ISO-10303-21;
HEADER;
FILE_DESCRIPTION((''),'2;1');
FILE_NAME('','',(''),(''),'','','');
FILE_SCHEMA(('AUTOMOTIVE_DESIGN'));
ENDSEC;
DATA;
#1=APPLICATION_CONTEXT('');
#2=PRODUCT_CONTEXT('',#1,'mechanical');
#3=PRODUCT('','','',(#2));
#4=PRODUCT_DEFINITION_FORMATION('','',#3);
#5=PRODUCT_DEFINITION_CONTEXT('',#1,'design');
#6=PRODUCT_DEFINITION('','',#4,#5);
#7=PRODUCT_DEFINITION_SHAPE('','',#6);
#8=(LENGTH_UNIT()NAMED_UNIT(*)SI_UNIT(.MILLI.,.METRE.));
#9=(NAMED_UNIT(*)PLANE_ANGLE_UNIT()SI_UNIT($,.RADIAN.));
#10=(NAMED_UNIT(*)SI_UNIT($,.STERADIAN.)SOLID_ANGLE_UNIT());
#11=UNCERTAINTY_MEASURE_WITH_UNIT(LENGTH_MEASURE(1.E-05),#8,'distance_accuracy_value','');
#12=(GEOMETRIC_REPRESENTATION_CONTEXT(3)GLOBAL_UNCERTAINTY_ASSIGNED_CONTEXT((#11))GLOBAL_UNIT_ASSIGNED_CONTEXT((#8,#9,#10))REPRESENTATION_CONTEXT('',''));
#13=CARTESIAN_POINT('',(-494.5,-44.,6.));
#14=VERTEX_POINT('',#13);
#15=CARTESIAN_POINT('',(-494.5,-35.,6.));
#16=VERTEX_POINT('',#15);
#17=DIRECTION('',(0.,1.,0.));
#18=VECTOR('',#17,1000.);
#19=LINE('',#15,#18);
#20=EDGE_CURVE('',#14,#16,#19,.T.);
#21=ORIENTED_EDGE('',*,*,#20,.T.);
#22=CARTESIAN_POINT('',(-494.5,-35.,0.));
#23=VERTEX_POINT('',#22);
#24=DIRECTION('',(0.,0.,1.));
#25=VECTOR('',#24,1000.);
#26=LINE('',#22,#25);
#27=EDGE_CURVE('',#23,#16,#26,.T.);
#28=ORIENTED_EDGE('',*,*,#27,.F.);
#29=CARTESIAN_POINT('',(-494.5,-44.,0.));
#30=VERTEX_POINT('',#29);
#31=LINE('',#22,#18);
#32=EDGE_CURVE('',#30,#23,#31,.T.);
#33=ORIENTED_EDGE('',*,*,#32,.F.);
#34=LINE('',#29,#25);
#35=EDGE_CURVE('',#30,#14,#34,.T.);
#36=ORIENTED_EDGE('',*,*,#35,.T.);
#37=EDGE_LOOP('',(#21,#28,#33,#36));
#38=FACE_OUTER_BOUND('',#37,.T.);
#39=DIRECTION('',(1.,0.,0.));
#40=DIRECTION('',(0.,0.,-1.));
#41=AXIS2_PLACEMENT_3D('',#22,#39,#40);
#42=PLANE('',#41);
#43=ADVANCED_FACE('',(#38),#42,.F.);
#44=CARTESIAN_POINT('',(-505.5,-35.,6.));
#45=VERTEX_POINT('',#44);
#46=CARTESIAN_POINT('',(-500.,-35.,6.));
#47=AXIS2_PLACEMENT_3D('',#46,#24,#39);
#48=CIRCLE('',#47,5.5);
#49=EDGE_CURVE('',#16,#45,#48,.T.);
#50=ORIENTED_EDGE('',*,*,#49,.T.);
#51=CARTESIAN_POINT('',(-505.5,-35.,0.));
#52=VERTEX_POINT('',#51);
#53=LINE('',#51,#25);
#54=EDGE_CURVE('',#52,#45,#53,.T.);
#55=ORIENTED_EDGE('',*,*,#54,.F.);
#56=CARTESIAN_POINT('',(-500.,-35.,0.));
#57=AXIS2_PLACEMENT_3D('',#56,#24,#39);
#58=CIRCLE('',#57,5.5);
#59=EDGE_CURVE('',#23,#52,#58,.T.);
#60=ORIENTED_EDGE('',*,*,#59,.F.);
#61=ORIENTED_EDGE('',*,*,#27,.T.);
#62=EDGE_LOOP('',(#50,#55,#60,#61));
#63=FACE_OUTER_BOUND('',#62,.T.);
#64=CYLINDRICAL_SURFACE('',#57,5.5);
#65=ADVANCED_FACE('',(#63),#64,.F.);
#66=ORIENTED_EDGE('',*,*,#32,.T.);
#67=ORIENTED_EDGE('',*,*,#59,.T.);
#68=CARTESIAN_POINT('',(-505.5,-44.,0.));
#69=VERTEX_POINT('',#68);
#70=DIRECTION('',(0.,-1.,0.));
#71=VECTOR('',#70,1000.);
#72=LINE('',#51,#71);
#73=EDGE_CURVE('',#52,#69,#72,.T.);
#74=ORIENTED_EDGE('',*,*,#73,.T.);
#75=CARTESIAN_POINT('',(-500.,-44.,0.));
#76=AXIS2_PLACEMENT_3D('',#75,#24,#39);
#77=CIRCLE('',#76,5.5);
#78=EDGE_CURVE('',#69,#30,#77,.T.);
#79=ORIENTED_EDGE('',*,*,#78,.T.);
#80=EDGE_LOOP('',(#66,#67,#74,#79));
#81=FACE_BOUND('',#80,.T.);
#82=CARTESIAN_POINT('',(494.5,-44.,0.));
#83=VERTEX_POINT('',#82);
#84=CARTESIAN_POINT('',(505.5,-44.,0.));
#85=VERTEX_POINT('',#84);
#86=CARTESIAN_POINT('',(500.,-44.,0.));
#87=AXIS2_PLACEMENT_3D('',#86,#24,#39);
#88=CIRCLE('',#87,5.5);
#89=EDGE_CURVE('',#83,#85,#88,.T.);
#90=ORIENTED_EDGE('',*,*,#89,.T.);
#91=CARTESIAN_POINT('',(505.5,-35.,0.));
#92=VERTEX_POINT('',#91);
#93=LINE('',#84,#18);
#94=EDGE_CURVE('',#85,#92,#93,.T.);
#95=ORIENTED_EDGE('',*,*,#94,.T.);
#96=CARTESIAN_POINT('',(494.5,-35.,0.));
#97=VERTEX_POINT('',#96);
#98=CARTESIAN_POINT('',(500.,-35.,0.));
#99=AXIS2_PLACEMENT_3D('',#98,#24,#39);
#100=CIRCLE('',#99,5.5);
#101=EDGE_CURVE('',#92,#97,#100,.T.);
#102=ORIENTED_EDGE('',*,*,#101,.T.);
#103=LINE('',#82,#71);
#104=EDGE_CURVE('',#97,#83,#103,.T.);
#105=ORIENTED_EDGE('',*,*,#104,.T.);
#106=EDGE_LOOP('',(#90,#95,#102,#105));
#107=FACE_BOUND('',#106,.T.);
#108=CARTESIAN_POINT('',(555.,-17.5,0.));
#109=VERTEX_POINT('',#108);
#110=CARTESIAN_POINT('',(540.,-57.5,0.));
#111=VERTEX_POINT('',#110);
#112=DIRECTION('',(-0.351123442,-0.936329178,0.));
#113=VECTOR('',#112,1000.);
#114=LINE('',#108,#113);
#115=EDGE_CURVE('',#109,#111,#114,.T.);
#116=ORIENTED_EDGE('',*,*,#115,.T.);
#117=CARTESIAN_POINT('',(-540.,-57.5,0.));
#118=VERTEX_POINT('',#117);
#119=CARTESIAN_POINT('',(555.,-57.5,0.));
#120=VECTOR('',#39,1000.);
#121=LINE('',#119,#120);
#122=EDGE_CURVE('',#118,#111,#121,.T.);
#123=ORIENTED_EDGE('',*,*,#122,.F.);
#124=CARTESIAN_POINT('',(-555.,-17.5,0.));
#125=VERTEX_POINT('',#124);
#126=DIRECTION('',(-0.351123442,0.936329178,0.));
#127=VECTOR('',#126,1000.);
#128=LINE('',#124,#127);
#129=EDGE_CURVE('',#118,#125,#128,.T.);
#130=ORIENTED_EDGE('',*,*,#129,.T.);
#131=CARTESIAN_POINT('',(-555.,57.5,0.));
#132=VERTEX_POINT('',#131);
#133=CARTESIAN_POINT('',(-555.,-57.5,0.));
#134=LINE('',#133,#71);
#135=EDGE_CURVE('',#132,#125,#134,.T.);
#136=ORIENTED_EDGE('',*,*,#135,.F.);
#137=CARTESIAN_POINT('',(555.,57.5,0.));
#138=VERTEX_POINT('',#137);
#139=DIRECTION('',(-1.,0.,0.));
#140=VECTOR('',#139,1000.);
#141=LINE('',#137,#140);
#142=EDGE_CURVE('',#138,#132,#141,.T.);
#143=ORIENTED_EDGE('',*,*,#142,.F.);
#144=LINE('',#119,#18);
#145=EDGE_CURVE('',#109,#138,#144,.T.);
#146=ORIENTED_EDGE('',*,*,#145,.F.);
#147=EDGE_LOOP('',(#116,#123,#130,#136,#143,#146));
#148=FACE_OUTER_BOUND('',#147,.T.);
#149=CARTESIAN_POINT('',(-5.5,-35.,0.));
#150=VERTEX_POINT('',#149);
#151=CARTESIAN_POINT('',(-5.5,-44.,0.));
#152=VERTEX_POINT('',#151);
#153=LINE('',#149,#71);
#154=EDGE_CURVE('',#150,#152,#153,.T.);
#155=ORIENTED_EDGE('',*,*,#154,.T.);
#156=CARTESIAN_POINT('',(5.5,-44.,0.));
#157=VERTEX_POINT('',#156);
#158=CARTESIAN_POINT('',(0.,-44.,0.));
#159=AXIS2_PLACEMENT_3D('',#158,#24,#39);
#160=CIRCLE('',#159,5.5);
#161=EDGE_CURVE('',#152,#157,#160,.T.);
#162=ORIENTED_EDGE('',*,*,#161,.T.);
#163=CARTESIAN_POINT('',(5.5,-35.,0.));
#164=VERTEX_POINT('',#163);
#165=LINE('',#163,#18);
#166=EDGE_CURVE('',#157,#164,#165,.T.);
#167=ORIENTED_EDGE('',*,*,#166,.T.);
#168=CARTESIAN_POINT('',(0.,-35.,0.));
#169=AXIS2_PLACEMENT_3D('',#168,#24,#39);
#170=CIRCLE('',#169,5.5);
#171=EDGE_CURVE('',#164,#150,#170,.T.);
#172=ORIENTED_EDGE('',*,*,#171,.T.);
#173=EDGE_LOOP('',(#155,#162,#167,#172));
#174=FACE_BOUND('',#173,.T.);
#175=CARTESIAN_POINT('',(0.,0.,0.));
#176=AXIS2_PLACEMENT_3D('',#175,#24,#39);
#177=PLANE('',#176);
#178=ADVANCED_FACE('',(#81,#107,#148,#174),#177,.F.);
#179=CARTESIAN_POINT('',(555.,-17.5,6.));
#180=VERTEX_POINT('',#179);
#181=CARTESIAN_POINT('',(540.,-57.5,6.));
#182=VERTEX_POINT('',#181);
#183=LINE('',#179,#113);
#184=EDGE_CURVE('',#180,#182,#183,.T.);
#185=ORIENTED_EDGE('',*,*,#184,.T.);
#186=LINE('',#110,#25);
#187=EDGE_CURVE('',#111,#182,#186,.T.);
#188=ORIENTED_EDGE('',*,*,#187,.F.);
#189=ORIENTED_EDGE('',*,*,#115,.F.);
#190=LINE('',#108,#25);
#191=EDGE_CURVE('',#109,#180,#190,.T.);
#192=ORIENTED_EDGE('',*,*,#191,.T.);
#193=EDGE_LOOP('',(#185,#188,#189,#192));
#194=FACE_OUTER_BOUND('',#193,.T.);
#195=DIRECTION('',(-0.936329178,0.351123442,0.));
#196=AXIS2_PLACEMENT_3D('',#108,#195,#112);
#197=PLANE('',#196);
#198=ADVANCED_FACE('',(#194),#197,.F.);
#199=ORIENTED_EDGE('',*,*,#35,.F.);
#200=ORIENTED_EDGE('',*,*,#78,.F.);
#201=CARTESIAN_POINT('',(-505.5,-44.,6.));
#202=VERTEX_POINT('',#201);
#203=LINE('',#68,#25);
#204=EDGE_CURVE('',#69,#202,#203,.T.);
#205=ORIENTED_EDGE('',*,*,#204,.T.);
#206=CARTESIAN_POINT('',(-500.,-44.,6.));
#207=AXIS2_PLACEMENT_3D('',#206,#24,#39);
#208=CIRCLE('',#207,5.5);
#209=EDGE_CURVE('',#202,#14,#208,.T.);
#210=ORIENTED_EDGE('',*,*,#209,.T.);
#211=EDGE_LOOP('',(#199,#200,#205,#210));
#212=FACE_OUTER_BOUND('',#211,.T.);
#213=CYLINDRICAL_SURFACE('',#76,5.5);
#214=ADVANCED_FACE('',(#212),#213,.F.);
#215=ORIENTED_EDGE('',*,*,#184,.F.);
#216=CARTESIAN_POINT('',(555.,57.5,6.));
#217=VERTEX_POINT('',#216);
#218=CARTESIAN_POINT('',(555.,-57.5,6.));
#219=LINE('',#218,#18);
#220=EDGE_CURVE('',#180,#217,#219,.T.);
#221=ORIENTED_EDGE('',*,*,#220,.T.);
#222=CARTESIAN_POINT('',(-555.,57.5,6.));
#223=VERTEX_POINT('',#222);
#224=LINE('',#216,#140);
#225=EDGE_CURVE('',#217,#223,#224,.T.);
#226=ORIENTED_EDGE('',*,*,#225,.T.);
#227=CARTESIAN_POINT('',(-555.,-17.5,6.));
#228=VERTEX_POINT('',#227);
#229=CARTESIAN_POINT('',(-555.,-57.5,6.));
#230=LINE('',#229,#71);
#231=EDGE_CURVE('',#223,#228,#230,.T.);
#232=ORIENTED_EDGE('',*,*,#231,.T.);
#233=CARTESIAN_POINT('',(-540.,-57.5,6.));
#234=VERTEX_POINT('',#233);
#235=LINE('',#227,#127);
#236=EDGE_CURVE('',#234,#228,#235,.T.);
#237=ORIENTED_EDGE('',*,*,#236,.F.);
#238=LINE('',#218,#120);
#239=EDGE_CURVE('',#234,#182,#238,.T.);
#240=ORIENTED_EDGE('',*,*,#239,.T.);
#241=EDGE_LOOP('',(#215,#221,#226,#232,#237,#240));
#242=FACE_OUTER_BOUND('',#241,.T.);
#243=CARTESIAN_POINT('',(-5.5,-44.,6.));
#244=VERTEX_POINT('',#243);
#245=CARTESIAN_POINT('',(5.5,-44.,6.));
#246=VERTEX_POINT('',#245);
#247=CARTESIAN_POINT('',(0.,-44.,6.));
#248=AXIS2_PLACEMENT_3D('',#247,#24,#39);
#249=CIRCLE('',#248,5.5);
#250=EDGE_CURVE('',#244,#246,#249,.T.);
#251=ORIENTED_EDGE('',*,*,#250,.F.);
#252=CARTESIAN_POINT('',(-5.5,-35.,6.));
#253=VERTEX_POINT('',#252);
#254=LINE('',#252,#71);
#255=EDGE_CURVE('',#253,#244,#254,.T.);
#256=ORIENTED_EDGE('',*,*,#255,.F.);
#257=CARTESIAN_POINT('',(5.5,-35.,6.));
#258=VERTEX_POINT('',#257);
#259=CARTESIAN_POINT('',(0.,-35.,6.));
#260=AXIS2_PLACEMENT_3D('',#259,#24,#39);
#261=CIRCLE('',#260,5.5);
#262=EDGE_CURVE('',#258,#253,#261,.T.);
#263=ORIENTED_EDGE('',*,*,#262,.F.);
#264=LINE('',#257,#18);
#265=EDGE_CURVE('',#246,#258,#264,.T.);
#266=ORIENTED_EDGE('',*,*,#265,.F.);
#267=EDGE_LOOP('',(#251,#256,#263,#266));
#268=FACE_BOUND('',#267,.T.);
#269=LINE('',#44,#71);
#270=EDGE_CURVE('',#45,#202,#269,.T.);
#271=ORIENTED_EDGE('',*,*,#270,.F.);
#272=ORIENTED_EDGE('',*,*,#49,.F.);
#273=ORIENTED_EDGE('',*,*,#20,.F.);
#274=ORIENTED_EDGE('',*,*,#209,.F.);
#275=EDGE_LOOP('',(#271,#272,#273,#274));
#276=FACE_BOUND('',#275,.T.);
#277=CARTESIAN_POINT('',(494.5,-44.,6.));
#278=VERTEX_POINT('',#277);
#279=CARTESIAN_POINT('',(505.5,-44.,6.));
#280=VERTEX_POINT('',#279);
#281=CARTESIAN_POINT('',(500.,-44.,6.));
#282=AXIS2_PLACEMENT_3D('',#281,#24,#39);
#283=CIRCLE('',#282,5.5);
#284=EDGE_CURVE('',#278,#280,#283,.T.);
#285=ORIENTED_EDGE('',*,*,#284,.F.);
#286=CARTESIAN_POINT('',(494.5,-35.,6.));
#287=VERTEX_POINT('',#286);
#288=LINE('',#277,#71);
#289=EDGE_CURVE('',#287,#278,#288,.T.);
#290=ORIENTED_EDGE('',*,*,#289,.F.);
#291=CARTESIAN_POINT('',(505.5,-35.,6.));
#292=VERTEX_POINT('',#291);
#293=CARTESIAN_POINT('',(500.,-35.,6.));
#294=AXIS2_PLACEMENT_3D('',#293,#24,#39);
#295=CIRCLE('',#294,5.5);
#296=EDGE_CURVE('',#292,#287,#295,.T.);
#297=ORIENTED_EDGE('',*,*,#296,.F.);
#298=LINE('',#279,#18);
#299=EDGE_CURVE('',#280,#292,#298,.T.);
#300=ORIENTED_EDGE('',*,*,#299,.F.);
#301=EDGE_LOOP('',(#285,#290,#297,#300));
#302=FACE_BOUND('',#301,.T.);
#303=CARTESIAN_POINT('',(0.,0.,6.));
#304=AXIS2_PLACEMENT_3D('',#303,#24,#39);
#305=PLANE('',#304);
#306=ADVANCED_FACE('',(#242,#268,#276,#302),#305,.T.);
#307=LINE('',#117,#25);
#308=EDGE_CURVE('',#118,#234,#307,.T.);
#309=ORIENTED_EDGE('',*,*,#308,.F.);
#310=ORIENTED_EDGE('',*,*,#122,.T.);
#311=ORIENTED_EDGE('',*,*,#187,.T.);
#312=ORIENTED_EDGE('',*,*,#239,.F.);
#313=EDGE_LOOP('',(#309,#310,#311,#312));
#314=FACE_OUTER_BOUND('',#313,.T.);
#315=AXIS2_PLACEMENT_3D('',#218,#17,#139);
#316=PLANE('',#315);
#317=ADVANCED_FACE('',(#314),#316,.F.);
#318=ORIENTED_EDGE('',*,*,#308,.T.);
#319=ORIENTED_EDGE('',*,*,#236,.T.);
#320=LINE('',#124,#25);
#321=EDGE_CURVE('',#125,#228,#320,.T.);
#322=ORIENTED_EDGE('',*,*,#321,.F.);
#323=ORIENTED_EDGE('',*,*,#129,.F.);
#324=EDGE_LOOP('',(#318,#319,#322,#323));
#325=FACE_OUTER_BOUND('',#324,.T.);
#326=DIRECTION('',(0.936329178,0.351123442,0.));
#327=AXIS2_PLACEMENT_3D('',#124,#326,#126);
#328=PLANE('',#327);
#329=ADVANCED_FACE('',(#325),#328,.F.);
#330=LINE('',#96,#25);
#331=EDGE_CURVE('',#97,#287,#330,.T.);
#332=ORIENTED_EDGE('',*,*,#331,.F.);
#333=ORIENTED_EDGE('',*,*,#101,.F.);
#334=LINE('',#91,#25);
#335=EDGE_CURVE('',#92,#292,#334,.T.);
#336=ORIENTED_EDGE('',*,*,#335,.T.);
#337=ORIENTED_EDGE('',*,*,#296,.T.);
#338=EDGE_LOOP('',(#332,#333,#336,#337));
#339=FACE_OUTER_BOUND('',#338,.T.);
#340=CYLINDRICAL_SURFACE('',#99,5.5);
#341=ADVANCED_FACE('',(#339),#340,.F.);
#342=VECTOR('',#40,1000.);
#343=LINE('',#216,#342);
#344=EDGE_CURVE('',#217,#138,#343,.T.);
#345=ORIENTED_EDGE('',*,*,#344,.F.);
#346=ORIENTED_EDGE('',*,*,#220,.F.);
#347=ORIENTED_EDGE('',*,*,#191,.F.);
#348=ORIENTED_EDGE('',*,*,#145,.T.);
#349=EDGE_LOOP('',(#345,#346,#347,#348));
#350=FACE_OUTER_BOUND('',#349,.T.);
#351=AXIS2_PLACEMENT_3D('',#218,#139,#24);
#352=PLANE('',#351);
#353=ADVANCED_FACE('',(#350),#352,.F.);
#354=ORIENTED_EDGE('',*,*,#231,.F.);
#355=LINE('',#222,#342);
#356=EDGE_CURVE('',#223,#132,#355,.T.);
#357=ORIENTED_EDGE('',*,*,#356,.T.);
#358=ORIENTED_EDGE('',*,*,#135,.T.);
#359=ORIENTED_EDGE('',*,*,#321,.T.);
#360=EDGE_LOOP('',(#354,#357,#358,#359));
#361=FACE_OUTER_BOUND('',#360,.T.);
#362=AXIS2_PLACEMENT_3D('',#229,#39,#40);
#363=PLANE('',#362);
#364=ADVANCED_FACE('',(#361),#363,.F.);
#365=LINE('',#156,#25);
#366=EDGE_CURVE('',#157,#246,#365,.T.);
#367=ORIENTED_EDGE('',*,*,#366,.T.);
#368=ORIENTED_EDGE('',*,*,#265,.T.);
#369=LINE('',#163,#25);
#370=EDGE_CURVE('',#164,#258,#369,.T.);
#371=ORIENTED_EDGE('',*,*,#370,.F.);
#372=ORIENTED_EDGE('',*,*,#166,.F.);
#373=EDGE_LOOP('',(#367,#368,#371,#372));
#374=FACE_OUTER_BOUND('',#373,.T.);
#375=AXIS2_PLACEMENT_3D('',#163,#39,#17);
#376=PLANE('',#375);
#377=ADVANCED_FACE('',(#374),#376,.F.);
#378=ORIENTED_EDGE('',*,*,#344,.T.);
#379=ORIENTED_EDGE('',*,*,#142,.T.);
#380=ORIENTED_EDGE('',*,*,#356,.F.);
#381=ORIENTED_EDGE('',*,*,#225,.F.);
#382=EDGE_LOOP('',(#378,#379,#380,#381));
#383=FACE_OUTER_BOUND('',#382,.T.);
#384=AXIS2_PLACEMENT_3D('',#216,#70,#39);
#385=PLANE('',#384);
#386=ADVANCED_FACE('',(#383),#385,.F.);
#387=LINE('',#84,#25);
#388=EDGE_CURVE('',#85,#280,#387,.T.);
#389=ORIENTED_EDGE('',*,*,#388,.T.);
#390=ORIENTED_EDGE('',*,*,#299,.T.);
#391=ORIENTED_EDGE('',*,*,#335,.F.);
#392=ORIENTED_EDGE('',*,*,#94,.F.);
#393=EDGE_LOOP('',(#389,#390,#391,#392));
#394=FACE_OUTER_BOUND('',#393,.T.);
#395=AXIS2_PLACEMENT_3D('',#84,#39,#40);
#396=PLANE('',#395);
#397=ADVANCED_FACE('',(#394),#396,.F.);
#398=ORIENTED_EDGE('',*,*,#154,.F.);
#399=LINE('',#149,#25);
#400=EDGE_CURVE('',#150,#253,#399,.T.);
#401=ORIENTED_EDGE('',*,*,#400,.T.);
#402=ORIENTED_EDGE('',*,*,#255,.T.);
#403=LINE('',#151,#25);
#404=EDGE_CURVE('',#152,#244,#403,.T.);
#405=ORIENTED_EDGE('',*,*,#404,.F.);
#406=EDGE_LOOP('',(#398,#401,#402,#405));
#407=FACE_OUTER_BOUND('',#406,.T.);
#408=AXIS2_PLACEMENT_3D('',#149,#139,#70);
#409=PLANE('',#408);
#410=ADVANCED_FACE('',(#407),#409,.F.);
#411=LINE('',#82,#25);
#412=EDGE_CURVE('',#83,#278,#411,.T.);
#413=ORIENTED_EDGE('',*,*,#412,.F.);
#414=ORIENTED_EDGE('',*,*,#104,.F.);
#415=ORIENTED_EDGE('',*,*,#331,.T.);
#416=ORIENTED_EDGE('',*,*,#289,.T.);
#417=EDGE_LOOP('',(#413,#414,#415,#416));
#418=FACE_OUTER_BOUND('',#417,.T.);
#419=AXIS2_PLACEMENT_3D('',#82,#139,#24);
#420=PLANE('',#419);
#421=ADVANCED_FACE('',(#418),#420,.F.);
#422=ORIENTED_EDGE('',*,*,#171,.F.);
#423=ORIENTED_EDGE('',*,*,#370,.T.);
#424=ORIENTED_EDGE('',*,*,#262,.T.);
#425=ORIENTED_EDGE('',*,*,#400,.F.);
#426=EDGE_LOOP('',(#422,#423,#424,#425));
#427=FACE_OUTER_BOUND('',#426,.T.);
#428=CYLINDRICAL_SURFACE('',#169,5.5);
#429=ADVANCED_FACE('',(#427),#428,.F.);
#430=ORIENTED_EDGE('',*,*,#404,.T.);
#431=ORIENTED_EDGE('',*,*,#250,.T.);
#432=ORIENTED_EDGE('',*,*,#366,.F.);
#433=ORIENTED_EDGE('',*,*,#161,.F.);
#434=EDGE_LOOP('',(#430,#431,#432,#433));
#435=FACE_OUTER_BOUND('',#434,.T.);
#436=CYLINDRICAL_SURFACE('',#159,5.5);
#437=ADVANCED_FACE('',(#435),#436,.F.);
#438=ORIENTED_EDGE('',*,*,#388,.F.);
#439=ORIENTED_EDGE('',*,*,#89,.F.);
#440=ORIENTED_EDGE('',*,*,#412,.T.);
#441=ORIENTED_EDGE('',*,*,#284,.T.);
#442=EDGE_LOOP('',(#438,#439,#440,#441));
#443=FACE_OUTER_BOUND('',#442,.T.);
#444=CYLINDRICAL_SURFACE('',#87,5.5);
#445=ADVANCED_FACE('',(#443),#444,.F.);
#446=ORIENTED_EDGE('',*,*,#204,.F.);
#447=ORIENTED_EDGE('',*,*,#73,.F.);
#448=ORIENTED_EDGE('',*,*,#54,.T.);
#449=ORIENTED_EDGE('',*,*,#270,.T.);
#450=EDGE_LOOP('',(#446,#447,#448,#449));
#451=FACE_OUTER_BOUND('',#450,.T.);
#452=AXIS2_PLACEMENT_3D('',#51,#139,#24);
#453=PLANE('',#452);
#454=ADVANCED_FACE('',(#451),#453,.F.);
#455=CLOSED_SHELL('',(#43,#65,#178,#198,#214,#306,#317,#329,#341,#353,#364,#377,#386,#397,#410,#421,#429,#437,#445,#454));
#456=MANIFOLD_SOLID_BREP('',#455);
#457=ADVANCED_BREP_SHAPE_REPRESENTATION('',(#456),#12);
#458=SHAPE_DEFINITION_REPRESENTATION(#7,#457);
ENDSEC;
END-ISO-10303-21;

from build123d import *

# Parameters (mm, degrees)
SKETCH1_W           = 1110
SKETCH1_H           = 115
BOSS_EXTRUDE1_DEPTH = 6
CUT_EXTRUDE1_DEPTH  = 6


with BuildPart() as part:
    # Sketch1 → Boss-Extrude1 (new body)
    with BuildSketch(Plane.XY):
        Rectangle(SKETCH1_W, SKETCH1_H)
    extrude(amount=BOSS_EXTRUDE1_DEPTH)

    # Sketch2 → Cut-Extrude1 (cut)
    with BuildSketch(Plane.XY.offset(6)):
        with BuildLine():
            Line((-494.5, -35), (-494.5, -44))
            ThreePointArc((-494.5, -44), (-500, -49.5), (-505.5, -44))
            Line((-505.5, -44), (-505.5, -35))
            ThreePointArc((-505.5, -35), (-500, -29.5), (-494.5, -35))
        make_face()
        with BuildLine():
            Line((5.5, -35), (5.5, -44))
            ThreePointArc((5.5, -44), (0, -49.5), (-5.5, -44))
            Line((-5.5, -44), (-5.5, -35))
            ThreePointArc((-5.5, -35), (0, -29.5), (5.5, -35))
        make_face()
        with BuildLine():
            Line((494.5, -44), (494.5, -35))
            ThreePointArc((494.5, -35), (500, -29.5), (505.5, -35))
            Line((505.5, -35), (505.5, -44))
            ThreePointArc((505.5, -44), (500, -49.5), (494.5, -44))
        make_face()
        Polygon((-555, -17.5), (-540, -57.5), (-555, -57.5), align=None)
        Polygon((555, -17.5), (540, -57.5), (555, -57.5), align=None)
    extrude(amount=-CUT_EXTRUDE1_DEPTH, mode=Mode.SUBTRACT)


solid = part.part
